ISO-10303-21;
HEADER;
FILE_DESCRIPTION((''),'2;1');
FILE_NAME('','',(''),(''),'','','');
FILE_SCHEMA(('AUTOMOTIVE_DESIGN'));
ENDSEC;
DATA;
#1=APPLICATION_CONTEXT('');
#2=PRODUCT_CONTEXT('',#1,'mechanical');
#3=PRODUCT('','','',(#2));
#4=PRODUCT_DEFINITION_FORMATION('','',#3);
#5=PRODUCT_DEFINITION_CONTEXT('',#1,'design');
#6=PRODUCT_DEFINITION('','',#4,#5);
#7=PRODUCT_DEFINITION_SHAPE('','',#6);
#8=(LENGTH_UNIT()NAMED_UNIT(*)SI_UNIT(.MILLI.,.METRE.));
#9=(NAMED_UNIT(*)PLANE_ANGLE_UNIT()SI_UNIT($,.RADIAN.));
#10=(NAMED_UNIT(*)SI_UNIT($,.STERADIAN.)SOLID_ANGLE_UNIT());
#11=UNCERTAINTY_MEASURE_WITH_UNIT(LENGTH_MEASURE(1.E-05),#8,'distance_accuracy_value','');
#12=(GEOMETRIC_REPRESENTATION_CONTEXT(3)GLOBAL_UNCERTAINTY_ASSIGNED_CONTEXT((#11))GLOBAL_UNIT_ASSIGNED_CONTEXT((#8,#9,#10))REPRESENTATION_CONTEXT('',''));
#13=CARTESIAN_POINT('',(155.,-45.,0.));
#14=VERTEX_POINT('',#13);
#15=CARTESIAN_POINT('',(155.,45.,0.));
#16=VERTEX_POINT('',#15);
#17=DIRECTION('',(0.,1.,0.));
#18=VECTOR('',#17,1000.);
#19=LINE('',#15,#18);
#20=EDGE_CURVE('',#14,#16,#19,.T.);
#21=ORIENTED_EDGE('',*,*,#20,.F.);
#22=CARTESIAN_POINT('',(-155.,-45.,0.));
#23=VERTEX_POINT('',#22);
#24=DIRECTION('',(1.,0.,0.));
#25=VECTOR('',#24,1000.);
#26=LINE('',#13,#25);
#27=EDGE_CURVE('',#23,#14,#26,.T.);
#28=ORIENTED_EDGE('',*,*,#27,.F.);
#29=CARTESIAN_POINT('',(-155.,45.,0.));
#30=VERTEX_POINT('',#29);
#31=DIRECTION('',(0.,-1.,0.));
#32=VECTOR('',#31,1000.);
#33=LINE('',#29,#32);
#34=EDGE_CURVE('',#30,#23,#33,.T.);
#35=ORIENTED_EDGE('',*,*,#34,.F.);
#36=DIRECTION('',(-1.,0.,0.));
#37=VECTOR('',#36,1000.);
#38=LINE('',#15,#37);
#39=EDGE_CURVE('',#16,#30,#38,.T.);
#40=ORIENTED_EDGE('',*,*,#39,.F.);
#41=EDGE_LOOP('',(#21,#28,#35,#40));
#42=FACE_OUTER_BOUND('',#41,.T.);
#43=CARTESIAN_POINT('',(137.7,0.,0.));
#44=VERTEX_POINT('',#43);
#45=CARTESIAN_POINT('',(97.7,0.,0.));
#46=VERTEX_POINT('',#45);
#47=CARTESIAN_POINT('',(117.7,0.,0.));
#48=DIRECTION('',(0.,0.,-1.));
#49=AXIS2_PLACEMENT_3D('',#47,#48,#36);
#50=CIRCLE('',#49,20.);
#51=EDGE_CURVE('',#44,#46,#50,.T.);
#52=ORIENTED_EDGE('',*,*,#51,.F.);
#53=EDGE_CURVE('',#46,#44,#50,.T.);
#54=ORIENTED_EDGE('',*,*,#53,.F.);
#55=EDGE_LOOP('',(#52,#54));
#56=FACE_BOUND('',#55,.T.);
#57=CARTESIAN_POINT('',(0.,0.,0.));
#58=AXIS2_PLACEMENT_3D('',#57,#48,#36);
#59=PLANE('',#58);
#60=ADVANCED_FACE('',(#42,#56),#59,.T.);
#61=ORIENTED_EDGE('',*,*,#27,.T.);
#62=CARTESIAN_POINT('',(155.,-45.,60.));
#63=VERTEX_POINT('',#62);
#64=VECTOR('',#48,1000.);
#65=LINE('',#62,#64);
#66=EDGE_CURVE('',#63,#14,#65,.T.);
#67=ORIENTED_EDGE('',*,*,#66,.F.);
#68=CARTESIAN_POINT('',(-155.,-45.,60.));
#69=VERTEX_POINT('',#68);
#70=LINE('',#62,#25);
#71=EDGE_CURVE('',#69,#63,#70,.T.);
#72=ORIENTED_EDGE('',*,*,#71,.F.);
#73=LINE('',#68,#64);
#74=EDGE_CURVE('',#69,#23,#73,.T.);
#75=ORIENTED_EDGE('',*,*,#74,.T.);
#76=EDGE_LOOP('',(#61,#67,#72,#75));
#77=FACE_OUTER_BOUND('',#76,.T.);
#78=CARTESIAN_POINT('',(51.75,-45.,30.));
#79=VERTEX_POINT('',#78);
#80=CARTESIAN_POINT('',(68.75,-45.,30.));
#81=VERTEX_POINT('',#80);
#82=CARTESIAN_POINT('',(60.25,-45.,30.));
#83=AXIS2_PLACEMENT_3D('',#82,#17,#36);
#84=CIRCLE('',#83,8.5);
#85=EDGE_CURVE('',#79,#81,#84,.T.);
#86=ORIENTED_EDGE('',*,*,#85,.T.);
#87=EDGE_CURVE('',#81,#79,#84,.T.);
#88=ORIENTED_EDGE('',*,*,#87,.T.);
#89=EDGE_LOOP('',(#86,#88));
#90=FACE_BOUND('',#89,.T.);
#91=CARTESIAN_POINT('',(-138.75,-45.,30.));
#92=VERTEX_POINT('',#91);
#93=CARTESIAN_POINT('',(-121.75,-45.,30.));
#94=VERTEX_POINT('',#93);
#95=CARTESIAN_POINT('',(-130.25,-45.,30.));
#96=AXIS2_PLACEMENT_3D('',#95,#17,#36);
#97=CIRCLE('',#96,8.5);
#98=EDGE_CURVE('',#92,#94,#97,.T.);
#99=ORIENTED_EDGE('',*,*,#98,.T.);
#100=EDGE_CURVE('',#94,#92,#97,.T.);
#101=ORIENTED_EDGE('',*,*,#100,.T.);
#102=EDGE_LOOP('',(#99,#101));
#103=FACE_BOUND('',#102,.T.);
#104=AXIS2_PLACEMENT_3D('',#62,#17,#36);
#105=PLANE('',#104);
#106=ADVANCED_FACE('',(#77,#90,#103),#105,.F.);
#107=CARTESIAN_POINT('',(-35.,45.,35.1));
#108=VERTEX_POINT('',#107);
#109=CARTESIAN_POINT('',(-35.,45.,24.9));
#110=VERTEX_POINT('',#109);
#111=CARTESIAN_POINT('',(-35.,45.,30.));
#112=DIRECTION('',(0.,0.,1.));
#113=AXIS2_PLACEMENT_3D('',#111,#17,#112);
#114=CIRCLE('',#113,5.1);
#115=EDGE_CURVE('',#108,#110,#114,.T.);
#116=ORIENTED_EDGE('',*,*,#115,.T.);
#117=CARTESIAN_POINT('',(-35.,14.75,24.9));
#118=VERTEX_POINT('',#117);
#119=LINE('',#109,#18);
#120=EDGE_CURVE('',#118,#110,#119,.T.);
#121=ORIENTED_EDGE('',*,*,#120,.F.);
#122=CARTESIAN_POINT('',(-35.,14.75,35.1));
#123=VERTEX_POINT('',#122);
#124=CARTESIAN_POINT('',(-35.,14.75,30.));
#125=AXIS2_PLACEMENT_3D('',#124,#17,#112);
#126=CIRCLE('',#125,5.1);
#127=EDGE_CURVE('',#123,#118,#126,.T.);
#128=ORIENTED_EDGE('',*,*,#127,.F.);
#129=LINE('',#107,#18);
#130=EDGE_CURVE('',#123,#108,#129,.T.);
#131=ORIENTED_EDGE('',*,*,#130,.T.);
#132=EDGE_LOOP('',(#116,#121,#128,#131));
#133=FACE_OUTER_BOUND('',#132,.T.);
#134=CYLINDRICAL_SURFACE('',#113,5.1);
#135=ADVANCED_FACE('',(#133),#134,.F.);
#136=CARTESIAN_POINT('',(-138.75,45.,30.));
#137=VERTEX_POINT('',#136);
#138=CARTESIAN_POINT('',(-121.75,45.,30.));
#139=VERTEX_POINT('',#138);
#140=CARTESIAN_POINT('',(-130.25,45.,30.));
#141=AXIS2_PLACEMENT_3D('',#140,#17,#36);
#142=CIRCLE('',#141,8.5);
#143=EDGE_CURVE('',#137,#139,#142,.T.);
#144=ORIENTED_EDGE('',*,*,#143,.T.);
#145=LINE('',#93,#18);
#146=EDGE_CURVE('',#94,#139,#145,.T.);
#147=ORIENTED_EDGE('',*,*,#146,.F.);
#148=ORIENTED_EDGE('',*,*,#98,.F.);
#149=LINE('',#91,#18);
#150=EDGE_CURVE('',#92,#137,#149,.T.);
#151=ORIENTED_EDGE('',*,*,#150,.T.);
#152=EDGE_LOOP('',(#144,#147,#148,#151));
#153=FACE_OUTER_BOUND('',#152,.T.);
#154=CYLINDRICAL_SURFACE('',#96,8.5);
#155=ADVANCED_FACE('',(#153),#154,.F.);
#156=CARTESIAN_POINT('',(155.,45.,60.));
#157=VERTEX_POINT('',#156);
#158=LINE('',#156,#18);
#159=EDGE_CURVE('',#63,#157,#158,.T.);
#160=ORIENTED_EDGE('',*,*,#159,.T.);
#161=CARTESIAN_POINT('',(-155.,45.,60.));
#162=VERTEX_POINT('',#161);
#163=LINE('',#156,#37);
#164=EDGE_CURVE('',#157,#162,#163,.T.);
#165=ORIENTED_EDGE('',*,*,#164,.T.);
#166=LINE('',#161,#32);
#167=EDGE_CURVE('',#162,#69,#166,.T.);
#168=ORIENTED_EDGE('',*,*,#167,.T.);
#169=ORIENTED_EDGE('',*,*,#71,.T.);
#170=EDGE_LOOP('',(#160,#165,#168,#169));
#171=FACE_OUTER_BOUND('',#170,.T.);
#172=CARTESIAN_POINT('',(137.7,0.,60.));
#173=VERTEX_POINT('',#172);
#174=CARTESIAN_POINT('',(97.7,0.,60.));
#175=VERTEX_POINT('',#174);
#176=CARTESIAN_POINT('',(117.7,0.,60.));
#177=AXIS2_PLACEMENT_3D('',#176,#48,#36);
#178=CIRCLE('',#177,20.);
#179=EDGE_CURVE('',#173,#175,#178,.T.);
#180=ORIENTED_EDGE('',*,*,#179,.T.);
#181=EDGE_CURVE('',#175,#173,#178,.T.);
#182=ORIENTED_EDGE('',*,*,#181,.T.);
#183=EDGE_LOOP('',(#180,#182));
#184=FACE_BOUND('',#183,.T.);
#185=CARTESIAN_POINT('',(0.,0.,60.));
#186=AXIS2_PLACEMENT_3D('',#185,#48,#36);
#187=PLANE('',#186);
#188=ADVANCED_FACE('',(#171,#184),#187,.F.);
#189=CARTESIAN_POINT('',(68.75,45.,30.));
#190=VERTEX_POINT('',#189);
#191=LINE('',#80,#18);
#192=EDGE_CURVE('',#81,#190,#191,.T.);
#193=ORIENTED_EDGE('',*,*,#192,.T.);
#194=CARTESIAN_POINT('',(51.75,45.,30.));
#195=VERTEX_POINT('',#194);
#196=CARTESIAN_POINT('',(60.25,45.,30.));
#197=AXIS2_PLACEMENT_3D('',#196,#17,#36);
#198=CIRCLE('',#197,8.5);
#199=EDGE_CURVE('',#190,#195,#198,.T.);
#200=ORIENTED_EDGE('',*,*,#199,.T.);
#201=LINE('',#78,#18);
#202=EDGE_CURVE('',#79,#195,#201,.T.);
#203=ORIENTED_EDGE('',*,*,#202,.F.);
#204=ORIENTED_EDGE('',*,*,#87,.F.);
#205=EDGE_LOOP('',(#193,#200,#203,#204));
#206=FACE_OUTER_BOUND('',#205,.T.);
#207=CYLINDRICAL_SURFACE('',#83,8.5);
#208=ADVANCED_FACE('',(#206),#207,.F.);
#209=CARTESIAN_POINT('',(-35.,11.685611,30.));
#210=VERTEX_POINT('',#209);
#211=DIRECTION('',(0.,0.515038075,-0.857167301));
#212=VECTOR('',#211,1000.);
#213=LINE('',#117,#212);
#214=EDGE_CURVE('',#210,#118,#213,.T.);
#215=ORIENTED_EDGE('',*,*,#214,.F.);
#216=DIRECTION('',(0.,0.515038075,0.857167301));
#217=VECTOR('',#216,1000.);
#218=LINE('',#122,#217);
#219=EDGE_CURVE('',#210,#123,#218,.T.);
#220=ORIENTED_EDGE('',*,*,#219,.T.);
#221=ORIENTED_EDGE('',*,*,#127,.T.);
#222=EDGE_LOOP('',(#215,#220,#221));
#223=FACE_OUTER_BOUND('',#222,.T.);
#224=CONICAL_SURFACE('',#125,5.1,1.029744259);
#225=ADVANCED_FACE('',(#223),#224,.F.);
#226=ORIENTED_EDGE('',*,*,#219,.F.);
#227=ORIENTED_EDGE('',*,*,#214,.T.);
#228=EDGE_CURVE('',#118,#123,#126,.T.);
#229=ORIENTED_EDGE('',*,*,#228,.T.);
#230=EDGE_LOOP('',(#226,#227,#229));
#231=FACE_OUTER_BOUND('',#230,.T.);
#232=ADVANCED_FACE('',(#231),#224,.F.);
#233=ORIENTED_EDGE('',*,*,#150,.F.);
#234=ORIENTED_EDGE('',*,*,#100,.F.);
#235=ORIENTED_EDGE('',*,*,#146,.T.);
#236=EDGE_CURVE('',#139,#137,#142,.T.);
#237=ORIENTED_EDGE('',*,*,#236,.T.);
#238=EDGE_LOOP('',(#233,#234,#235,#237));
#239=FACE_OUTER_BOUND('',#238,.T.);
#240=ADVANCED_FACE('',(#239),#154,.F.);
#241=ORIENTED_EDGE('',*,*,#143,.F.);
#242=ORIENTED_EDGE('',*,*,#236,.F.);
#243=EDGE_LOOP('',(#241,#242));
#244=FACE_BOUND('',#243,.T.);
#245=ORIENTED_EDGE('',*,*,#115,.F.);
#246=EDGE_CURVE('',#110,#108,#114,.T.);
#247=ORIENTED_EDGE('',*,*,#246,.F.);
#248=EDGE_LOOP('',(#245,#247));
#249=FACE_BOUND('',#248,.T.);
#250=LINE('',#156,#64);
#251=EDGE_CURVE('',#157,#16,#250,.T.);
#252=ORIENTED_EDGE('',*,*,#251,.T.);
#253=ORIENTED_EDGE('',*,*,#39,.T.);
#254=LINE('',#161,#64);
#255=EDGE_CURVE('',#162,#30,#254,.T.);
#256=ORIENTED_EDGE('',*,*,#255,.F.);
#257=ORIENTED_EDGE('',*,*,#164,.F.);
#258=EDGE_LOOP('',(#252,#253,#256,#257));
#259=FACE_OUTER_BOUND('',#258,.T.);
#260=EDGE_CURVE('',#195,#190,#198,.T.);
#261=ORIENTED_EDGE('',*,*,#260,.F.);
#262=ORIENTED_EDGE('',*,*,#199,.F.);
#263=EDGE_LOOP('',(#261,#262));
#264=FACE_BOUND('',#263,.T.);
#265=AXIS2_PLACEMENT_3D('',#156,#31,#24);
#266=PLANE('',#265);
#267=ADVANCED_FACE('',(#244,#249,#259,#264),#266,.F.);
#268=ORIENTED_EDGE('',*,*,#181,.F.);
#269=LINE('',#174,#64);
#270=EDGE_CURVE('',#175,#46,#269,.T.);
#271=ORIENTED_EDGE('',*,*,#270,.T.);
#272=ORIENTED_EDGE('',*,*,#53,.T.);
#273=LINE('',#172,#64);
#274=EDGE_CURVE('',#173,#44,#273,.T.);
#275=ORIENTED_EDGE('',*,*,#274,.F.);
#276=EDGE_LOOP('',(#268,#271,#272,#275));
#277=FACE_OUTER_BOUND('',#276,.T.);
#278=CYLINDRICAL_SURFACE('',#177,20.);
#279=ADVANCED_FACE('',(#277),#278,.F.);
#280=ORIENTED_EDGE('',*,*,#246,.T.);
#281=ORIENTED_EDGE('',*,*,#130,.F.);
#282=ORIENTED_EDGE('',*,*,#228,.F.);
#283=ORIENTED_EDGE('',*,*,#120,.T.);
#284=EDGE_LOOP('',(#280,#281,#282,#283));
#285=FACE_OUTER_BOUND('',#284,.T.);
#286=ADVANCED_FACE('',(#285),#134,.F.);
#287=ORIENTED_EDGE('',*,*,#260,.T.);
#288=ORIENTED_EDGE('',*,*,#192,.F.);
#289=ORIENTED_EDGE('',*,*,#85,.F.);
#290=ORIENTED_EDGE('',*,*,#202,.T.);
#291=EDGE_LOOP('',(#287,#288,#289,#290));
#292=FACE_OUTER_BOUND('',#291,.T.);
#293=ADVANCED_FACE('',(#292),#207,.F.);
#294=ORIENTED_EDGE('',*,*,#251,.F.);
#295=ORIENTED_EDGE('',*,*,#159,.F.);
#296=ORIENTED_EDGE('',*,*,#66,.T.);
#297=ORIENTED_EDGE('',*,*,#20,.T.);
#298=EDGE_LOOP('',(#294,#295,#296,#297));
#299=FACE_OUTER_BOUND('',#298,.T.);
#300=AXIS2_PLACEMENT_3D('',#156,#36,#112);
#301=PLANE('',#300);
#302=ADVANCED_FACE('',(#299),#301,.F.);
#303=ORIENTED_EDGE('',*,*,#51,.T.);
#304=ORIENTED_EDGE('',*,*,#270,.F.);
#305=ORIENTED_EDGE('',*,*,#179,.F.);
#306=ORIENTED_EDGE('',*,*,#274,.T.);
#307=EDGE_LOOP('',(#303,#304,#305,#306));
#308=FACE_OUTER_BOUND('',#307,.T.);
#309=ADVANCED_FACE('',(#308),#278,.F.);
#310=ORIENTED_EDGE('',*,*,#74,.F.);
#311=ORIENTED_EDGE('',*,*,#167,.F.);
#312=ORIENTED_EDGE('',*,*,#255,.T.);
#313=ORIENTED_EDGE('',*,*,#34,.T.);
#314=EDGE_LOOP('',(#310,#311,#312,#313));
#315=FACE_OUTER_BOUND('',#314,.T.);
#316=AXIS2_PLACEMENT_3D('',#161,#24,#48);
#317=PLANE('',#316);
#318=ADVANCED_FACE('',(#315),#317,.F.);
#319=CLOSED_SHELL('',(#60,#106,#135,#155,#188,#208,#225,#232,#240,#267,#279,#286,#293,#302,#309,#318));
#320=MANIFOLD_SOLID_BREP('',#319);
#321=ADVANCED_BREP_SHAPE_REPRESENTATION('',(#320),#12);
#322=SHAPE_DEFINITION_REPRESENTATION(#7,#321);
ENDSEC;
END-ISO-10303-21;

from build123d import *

# Parameters (mm, degrees)
SKETCH_1_W              = 310
SKETCH_1_H              = 90
EXTRUDE_1_DEPTH         = 60
SKETCH_2_R              = 8.5
CUT_EXTRUDE_1_DEPTH     = 90
HOLE_WIZARD_M12_1_D     = 10.2
HOLE_WIZARD_M12_1_DEPTH = 30.25
HOLE_WIZARD_M12_1_TIP   = 3.064389157
SKETCH_6_R              = 20
CUT_EXTRUDE_2_DEPTH     = 60


with BuildPart() as part:
    # 草图1 → 凸台-拉伸1 (new body)
    with BuildSketch(Plane.XY):
        Rectangle(SKETCH_1_W, SKETCH_1_H)
    extrude(amount=EXTRUDE_1_DEPTH)

    # 草图2 → 切除-拉伸1 (cut)
    with BuildSketch(Plane(origin=(0, 45, 0), x_dir=(1, 0, 0), z_dir=(0, 1, 0))):
        with Locations(Location((-130.25, -30, 0), (0, 0, 180))):
            Circle(SKETCH_2_R)
        with Locations(Location((60.25, -30, 0), (0, 0, 180))):
            Circle(SKETCH_2_R)
    extrude(amount=-CUT_EXTRUDE_1_DEPTH, mode=Mode.SUBTRACT)

    # M12 螺纹孔1
    with Locations(Plane(origin=(0, 45, 0), x_dir=(1, 0, 0), z_dir=(0, 1, 0))):
        with Locations((-35, -30)):
            Hole(HOLE_WIZARD_M12_1_D / 2, depth=HOLE_WIZARD_M12_1_DEPTH)
            with Locations((0, 0, -(HOLE_WIZARD_M12_1_DEPTH + HOLE_WIZARD_M12_1_TIP / 2))):  # 118° drill point
                Cone(0, HOLE_WIZARD_M12_1_D / 2, HOLE_WIZARD_M12_1_TIP, mode=Mode.SUBTRACT)

    # 草图6 → 切除-拉伸2 (cut)
    with BuildSketch(Plane(origin=(0, 0, 0), x_dir=(-1, 0, 0), z_dir=(0, 0, -1))):
        with Locations((-117.7, 0)):
            Circle(SKETCH_6_R)
    extrude(amount=-CUT_EXTRUDE_2_DEPTH, mode=Mode.SUBTRACT)


solid = part.part
